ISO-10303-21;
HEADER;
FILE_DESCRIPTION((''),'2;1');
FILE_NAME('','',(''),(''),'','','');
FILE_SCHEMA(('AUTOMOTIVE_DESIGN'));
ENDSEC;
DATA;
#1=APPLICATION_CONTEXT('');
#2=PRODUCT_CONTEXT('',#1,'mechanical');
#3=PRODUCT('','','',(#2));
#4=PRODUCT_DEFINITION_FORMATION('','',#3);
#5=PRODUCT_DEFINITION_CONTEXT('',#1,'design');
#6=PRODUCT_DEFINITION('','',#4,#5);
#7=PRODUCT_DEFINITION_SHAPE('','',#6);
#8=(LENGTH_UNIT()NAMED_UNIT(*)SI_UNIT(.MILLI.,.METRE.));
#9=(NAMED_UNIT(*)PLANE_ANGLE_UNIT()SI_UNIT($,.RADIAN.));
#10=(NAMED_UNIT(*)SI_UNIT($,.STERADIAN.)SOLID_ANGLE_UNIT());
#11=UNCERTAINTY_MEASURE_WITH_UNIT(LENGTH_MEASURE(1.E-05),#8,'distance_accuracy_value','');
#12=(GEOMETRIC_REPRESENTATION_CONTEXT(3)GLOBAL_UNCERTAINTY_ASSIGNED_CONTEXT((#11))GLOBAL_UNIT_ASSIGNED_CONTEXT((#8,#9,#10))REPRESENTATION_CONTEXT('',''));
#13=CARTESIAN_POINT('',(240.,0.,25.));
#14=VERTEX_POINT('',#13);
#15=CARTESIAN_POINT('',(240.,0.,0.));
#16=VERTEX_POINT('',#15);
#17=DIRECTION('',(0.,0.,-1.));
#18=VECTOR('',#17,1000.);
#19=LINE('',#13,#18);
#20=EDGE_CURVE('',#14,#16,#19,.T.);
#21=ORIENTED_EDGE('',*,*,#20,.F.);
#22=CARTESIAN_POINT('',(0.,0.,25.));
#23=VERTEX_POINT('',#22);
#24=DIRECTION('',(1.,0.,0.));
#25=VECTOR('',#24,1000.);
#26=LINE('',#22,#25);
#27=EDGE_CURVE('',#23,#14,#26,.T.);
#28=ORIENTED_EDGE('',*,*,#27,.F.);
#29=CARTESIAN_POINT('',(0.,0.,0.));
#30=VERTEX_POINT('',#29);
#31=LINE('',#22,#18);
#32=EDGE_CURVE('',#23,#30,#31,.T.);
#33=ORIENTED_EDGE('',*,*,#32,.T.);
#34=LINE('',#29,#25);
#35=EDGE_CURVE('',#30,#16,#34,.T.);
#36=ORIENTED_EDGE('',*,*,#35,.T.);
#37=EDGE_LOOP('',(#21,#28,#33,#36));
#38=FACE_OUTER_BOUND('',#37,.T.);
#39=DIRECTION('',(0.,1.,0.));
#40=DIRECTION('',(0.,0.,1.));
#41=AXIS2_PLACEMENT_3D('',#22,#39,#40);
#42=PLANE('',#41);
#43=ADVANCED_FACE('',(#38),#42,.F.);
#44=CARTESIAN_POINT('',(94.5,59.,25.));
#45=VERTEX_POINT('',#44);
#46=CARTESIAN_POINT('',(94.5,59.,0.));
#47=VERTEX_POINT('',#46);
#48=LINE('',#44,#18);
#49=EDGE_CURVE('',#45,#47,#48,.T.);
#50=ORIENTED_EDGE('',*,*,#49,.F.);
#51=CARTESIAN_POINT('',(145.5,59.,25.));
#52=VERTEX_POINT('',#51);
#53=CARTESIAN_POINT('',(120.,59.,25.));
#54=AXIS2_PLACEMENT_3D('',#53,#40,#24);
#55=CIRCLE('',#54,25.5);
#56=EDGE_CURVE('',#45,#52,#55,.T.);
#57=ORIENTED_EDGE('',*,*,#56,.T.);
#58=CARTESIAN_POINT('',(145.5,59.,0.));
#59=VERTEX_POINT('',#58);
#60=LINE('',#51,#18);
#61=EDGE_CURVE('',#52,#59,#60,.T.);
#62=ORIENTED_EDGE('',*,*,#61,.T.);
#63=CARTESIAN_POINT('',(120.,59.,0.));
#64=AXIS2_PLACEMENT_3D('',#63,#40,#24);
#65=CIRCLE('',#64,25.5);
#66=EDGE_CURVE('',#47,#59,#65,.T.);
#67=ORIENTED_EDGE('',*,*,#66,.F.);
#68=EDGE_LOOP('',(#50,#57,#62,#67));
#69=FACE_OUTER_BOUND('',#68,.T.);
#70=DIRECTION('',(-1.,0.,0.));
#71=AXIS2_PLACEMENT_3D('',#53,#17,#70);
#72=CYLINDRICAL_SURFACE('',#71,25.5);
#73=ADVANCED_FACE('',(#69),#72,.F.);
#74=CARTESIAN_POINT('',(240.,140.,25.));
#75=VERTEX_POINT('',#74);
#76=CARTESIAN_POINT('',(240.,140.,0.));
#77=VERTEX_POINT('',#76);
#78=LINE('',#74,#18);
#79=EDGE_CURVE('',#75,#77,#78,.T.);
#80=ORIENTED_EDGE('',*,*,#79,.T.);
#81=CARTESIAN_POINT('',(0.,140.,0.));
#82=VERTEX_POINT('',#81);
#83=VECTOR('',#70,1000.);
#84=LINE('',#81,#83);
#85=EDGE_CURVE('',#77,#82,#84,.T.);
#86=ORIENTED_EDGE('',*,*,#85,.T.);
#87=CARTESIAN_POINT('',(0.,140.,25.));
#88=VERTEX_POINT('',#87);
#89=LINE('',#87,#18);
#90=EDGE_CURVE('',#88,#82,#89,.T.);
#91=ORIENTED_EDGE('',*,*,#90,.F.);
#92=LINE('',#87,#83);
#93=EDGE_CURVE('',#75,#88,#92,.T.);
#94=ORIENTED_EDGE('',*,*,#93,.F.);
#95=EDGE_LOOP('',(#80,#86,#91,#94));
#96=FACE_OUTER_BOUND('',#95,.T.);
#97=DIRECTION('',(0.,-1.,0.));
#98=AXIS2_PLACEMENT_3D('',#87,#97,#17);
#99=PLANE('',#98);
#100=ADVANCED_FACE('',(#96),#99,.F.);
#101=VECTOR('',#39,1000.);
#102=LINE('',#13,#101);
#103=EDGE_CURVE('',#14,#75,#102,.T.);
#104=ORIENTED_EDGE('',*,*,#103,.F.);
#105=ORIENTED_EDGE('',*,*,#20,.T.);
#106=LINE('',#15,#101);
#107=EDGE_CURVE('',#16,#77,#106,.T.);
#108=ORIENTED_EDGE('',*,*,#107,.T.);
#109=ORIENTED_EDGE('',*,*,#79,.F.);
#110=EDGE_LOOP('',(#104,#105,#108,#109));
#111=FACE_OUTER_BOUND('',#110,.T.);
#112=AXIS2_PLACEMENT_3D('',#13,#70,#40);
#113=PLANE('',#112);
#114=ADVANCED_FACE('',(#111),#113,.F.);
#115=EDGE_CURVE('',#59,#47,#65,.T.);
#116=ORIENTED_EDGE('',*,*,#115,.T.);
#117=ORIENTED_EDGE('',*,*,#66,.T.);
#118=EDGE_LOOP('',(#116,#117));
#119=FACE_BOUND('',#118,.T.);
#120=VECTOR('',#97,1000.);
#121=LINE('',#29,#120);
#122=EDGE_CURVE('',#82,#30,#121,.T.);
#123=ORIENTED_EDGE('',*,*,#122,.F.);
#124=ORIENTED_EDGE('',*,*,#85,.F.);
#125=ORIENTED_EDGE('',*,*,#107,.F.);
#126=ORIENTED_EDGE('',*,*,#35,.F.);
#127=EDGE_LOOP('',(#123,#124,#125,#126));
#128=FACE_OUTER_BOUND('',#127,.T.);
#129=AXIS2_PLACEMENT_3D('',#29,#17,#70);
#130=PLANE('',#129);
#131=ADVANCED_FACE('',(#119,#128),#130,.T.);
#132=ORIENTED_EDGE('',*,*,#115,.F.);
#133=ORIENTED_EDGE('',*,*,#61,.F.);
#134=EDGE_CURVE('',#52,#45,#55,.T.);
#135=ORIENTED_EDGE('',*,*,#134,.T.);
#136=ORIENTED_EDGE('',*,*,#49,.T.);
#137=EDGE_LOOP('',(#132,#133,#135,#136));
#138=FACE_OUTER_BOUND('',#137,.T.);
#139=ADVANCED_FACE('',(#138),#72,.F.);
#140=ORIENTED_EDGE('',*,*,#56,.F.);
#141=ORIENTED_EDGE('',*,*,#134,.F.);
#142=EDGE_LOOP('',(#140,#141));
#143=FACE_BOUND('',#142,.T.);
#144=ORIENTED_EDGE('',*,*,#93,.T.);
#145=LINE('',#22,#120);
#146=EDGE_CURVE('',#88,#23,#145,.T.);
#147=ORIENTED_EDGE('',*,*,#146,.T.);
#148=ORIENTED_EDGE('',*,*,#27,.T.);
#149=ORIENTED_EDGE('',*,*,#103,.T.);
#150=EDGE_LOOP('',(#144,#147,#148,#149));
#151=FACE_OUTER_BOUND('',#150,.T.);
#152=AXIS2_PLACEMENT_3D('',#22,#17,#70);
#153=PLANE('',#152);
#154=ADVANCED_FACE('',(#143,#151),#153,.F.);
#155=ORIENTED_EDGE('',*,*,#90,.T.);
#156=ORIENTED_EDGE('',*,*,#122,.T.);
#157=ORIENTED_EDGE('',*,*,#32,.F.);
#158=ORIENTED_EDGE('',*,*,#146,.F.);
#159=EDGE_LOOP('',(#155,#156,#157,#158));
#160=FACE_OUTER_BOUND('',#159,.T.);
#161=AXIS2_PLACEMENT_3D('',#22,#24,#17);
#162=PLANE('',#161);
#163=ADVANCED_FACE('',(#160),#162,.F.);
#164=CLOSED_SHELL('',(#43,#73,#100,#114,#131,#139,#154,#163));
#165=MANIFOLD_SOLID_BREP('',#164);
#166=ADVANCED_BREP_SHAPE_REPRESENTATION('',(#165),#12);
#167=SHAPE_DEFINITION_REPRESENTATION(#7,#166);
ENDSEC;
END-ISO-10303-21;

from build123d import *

# Parameters (mm, degrees)
SKETCH1_W           = 240
SKETCH1_H           = 140
SKETCH1_R           = 25.5
BOSS_EXTRUDE1_DEPTH = 25


with BuildPart() as part:
    # Sketch1 → Boss-Extrude1 (new body)
    with BuildSketch(Plane.XY):
        with Locations((120, 70)):
            Rectangle(SKETCH1_W, SKETCH1_H)
        with Locations((120, 59)):
            Circle(SKETCH1_R, mode=Mode.SUBTRACT)
    extrude(amount=BOSS_EXTRUDE1_DEPTH)


solid = part.part
